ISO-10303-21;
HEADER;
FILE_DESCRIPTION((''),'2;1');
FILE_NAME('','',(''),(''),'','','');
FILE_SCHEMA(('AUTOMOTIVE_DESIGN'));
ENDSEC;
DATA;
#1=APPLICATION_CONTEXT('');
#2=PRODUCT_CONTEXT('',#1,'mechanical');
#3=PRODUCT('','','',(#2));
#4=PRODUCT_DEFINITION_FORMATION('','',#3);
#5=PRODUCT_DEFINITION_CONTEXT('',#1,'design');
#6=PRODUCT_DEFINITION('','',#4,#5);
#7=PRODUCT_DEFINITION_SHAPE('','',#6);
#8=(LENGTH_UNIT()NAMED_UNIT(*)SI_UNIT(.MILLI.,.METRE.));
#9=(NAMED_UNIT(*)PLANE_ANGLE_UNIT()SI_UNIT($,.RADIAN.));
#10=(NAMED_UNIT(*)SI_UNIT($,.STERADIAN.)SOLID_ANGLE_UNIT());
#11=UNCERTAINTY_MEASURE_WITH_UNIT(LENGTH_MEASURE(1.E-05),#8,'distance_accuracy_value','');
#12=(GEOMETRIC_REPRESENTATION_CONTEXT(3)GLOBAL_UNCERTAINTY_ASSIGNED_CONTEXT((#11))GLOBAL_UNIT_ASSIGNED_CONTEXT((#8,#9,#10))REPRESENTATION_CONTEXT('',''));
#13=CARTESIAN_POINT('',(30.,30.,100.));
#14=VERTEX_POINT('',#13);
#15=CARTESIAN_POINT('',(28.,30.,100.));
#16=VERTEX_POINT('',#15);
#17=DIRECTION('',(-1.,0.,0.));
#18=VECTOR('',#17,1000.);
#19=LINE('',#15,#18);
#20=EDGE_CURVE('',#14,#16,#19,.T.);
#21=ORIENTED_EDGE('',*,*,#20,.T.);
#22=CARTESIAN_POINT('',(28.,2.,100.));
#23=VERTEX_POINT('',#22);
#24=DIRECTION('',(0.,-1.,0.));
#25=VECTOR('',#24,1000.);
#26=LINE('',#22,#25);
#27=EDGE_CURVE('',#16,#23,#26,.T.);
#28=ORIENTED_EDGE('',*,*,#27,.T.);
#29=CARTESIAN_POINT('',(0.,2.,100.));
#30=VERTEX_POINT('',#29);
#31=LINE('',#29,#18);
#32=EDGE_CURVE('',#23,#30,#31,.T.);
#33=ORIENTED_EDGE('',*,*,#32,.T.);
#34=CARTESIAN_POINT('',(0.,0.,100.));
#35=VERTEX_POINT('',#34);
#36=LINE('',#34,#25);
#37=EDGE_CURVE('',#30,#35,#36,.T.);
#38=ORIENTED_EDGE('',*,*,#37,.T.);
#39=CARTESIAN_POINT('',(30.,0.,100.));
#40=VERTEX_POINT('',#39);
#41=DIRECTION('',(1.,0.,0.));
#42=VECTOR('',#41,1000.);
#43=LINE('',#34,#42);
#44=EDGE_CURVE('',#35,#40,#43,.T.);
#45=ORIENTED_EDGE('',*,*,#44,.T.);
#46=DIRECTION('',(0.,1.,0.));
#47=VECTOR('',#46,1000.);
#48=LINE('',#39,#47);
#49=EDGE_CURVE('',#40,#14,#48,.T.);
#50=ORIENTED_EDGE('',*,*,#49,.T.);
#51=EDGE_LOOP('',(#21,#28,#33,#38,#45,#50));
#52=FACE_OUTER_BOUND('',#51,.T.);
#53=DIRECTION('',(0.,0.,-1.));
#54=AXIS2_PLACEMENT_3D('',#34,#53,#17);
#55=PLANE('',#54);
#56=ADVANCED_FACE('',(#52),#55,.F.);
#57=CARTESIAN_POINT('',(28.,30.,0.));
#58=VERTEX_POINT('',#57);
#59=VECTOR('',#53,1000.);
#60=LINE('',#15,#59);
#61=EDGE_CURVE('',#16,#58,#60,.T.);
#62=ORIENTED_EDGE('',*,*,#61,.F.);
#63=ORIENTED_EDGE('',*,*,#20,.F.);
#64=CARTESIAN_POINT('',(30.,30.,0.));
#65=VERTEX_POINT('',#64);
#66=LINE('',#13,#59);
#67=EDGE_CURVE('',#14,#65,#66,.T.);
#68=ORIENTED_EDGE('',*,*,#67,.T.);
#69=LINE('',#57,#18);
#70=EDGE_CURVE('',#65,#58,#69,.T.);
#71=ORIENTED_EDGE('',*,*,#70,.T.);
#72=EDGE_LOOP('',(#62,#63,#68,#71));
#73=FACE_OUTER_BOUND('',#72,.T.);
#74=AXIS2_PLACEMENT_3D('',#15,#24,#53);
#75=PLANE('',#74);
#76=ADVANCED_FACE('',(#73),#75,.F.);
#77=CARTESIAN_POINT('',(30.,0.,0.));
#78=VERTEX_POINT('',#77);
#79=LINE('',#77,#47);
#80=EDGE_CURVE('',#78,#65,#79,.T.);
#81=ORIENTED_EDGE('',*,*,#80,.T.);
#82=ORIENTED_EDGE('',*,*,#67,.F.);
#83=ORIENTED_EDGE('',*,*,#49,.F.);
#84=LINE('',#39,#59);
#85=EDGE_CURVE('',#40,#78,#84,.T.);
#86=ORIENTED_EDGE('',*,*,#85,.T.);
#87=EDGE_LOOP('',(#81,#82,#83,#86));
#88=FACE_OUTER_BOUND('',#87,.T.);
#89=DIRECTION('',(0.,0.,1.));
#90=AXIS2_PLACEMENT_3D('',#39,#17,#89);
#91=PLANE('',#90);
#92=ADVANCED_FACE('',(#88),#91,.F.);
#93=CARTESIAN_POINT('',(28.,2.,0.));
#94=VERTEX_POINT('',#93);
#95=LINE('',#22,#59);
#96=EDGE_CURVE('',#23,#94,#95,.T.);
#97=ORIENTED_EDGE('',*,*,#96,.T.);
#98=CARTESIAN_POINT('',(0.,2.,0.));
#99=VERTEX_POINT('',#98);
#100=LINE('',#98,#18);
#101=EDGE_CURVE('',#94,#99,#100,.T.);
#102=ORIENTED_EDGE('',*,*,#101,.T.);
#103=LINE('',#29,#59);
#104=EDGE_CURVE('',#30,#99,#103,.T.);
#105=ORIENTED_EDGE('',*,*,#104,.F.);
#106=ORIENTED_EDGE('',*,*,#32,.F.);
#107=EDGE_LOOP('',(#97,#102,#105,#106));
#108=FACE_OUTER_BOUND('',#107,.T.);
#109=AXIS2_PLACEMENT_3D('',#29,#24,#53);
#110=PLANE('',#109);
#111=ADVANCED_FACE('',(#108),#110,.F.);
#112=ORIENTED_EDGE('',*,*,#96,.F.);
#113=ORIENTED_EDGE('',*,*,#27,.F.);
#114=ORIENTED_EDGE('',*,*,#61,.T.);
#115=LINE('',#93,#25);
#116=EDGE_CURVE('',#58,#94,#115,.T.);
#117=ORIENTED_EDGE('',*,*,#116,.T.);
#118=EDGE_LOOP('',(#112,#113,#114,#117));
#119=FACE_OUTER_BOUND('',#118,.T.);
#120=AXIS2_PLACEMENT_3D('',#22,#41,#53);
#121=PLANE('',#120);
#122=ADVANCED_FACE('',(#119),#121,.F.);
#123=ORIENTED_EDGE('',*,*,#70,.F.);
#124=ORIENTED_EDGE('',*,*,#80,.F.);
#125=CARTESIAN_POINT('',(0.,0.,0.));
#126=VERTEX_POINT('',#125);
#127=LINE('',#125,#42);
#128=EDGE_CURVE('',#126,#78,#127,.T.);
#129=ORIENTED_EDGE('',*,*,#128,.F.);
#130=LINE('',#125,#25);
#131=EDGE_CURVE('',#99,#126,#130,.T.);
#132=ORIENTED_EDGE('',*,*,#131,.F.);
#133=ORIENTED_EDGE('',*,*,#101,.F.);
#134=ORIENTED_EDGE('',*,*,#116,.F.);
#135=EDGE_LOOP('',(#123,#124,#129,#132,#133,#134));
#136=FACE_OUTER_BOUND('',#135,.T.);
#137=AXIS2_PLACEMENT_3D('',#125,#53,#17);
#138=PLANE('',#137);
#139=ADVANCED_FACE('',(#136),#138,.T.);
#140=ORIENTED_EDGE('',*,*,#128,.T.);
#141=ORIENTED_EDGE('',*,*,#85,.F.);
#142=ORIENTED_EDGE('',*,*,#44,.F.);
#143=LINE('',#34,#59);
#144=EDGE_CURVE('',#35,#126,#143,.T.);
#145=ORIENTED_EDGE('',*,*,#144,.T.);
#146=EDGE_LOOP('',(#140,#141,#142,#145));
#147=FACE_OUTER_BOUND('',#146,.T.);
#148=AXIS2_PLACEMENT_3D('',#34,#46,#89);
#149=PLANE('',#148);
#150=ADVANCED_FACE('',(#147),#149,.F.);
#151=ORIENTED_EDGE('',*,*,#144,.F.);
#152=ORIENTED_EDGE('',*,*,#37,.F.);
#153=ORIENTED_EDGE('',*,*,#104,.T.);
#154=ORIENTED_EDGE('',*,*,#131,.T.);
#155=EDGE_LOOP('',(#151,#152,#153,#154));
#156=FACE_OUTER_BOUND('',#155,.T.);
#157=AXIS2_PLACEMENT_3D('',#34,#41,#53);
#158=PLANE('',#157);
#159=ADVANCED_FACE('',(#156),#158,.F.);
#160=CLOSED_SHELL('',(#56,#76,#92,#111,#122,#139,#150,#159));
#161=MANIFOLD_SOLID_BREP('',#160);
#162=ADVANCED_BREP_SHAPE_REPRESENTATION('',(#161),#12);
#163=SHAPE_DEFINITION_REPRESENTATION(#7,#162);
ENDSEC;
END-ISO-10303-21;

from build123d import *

# Parameters (mm, degrees)
EXTRUDE_2_DEPTH = 100


with BuildPart() as part:
    # 草图1 → 凸台-拉伸2 (new body)
    with BuildSketch(Plane.XY):
        Polygon((0, 0), (30, 0), (30, 30), (28, 30), (28, 2), (0, 2), align=None)
    extrude(amount=EXTRUDE_2_DEPTH)


solid = part.part
